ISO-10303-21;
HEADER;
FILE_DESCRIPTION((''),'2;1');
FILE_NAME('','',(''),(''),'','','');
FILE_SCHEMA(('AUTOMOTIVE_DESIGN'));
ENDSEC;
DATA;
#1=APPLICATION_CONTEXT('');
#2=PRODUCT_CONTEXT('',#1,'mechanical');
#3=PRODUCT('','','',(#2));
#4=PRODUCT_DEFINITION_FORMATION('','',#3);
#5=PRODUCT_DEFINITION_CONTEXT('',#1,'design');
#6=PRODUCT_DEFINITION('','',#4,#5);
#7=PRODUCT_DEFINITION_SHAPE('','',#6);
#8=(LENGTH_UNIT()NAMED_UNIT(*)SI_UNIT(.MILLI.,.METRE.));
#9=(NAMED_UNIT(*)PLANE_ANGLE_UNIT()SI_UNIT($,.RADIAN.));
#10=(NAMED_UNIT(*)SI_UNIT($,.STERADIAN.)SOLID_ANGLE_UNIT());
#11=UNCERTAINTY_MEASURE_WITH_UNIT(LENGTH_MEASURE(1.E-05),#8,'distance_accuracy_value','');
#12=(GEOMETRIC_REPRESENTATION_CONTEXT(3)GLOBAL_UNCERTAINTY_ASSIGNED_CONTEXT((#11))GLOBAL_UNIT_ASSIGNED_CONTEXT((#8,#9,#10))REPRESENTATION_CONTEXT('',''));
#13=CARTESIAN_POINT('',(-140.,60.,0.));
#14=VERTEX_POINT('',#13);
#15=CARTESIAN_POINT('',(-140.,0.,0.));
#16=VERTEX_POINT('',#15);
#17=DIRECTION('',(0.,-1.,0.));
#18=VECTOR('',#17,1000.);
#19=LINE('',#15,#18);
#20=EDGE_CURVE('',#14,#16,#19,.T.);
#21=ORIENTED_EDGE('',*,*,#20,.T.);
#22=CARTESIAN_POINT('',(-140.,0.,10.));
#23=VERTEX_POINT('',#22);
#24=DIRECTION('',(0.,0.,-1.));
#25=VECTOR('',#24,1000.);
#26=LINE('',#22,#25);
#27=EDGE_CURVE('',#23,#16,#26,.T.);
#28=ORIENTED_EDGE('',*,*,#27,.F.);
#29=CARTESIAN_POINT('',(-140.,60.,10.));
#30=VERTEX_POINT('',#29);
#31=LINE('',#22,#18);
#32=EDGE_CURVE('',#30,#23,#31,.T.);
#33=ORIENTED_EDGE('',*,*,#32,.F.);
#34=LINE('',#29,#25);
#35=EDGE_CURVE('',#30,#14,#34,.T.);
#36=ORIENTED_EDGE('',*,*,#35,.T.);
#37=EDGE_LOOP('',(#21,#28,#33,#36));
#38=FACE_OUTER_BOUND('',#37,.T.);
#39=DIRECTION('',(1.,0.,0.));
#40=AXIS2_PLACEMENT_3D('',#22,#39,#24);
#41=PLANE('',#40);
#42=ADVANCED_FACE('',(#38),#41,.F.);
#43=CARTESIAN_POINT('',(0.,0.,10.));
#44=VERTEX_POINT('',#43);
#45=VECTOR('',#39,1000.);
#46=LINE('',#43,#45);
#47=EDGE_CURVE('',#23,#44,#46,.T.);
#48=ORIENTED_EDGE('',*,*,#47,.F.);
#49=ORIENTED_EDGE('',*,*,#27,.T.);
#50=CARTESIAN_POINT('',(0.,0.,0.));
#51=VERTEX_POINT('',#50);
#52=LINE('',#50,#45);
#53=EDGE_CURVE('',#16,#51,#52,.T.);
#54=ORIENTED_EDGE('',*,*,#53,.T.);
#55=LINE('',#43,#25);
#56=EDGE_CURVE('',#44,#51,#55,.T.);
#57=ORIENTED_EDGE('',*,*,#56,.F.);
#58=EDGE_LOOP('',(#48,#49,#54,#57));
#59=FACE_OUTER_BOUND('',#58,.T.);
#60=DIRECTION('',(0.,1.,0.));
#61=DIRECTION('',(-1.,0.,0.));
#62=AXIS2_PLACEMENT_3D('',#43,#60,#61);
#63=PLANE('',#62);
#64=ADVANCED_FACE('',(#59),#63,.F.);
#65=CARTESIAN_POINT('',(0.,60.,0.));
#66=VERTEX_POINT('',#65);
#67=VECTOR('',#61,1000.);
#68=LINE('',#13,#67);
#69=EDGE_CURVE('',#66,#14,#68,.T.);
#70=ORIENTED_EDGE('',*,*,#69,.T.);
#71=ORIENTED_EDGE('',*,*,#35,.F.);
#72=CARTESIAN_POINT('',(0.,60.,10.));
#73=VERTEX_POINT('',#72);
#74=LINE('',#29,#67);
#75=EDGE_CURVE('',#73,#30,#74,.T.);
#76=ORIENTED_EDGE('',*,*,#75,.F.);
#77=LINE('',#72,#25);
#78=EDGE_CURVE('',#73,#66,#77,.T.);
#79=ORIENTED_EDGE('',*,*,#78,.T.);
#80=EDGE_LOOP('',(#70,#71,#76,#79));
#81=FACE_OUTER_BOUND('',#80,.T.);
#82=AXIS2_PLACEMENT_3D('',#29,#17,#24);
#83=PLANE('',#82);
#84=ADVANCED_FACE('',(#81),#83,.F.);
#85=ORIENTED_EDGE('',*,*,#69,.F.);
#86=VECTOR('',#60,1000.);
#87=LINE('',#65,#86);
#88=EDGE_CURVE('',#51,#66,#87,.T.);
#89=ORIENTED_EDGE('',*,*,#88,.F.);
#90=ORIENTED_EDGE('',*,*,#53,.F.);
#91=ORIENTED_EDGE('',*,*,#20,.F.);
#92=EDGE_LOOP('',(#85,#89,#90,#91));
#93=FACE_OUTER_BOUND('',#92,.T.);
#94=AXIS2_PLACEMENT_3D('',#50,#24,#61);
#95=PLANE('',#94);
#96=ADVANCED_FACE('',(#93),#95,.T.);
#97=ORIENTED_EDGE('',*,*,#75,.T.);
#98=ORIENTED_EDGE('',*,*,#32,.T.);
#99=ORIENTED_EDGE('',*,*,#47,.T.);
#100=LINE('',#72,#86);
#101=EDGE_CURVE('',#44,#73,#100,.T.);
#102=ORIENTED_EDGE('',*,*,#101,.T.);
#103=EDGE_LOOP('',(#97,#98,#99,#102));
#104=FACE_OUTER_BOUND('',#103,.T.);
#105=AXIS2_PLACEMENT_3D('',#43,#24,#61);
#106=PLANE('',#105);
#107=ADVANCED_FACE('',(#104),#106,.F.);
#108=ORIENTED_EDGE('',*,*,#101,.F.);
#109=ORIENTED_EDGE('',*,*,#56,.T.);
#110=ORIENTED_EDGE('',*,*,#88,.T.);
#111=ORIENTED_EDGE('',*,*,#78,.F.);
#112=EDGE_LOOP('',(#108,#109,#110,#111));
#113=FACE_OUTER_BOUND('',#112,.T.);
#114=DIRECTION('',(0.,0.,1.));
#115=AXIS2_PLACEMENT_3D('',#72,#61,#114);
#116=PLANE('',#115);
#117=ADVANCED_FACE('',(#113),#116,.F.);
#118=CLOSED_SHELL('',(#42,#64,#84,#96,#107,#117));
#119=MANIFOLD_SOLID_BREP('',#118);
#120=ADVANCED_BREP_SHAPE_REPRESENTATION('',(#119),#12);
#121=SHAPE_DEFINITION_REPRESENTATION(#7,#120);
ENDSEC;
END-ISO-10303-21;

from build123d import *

# Parameters (mm, degrees)
SKETCH_1_W      = 140
SKETCH_1_H      = 60
EXTRUDE_1_DEPTH = 10


with BuildPart() as part:
    # 草图1 → 凸台-拉伸1 (new body)
    with BuildSketch(Plane.XY):
        with Locations((-70, 30)):
            Rectangle(SKETCH_1_W, SKETCH_1_H)
    extrude(amount=EXTRUDE_1_DEPTH)


solid = part.part
